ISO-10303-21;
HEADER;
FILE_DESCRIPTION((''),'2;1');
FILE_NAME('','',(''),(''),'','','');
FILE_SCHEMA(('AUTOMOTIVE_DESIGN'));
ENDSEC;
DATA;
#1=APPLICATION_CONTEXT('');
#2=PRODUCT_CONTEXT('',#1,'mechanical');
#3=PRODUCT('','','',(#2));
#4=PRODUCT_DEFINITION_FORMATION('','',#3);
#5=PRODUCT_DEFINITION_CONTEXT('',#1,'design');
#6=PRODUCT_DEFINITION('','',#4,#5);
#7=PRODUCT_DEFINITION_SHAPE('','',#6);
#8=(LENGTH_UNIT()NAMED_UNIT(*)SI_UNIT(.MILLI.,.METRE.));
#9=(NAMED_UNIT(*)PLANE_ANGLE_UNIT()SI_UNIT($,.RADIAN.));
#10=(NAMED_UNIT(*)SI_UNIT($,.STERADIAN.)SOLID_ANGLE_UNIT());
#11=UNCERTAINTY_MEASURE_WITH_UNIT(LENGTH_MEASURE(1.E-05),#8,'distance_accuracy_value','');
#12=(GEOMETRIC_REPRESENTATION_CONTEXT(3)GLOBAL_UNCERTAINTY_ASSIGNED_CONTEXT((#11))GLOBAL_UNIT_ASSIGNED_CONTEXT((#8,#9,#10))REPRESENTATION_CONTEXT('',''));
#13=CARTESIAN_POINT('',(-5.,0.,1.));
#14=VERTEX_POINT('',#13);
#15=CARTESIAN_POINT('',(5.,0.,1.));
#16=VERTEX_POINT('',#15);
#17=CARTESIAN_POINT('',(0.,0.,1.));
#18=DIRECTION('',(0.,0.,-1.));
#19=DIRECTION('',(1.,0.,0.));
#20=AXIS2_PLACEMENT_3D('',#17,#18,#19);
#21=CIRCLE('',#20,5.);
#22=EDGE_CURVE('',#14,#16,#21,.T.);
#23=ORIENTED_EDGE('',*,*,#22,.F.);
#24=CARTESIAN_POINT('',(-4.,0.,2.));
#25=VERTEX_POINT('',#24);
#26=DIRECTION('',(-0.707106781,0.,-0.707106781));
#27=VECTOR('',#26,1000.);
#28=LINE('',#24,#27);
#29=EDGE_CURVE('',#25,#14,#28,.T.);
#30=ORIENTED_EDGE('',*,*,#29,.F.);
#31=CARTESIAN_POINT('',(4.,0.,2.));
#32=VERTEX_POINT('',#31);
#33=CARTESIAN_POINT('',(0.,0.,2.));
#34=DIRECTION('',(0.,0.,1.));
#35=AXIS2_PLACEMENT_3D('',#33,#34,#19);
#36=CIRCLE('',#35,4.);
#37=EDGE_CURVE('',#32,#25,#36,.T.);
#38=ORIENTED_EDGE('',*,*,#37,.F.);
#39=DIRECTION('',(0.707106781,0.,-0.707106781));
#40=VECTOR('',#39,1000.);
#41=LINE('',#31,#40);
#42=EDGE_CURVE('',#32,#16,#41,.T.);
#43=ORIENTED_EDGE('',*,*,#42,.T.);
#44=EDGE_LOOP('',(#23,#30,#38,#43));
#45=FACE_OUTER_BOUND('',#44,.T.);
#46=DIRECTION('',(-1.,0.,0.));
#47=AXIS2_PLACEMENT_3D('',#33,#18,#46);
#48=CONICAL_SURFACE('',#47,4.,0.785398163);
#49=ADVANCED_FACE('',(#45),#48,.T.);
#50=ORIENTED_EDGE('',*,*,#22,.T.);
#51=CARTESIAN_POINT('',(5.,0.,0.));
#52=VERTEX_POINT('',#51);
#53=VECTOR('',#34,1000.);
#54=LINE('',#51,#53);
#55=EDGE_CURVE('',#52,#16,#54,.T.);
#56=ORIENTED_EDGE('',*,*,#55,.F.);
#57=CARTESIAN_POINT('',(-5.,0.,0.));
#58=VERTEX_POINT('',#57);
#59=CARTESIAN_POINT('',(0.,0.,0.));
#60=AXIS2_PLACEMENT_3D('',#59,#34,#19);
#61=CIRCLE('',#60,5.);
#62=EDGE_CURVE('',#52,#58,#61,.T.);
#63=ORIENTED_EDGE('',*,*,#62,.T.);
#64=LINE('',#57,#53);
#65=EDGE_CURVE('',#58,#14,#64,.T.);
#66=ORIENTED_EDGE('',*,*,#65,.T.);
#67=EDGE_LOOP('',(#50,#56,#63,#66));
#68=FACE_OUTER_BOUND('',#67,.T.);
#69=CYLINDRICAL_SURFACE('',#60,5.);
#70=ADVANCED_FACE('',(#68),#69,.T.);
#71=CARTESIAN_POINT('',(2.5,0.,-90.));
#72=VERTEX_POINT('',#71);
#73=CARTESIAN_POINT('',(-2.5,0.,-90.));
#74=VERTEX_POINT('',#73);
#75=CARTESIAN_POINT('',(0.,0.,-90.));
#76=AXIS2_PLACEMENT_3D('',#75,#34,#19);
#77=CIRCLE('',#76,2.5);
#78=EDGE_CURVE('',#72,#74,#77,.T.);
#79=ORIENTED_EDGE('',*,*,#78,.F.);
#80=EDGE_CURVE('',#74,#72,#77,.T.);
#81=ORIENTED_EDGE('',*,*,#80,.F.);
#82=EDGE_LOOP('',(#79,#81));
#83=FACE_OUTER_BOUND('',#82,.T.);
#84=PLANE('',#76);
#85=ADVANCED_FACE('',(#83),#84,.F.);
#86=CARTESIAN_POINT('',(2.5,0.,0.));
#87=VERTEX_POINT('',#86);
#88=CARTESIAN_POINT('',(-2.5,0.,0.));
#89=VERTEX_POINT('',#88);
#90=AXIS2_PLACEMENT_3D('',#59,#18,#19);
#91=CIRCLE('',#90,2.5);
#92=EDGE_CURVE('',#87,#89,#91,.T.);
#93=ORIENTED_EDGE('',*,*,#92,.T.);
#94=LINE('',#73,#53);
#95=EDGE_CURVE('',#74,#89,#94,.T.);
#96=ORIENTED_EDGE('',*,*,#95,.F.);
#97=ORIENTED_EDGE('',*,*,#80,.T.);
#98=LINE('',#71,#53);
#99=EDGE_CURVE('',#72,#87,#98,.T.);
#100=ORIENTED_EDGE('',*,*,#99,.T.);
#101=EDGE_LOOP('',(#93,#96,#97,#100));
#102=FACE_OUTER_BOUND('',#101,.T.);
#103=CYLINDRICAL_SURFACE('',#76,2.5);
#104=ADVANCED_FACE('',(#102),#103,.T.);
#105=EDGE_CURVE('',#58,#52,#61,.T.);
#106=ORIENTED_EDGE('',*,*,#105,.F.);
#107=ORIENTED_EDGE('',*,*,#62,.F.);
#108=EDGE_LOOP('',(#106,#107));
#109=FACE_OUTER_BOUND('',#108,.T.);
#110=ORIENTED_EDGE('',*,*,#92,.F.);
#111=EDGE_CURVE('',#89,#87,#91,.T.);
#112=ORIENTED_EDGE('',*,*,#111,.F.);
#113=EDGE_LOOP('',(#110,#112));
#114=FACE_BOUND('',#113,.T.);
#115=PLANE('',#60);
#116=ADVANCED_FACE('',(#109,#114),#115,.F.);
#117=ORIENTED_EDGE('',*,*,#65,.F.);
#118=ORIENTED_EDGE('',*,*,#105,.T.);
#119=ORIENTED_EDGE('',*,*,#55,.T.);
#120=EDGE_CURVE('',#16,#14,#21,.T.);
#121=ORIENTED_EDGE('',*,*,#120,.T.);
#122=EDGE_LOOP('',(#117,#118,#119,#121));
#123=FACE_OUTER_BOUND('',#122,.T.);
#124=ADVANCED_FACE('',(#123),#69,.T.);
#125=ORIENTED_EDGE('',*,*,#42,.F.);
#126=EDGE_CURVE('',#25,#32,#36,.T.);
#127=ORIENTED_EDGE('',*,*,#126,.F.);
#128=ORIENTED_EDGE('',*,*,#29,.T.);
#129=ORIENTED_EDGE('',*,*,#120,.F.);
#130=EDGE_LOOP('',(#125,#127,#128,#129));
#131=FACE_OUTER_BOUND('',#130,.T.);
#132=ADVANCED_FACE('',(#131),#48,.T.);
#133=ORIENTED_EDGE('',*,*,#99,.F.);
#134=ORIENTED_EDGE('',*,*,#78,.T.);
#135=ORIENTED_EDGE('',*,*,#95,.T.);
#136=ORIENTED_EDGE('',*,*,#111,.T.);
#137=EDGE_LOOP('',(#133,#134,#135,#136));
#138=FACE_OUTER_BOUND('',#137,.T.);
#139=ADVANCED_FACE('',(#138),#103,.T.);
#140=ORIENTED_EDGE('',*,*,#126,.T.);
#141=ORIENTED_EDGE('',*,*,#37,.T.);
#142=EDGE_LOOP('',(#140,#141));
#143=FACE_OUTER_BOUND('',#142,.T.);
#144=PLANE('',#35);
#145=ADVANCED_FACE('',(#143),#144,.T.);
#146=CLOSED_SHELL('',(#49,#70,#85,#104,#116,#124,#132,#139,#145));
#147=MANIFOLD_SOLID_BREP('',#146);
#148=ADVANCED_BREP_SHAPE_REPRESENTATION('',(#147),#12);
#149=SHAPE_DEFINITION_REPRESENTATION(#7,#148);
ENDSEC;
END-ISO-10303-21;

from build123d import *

# Parameters (mm, degrees)
BOSS_EXTRUDE1_DEPTH      = 2
BOSS_EXTRUDE1_DEPTH_BACK = 90
SKETCH1_R                = 2.5
SKETCH2_R                = 5
BOSS_EXTRUDE2_DEPTH      = 2
CHAMFER1_SIZE            = 1


with BuildPart() as part:
    # Sketch1 → Boss-Extrude1 (new, two sides: drawn at the far end of the back side and taken through both)
    with BuildSketch(Plane.XY.offset(-BOSS_EXTRUDE1_DEPTH_BACK)):
        Circle(SKETCH1_R)
    extrude(amount=BOSS_EXTRUDE1_DEPTH + BOSS_EXTRUDE1_DEPTH_BACK)

    # Sketch2 → Boss-Extrude2 (add)
    with BuildSketch(Plane.XY.offset(2)):
        Circle(SKETCH2_R)
    extrude(amount=-BOSS_EXTRUDE2_DEPTH)

    # Chamfer1
    chamfer1_edges = [part.edges().sort_by_distance(p)[0] for p in [
        (-5, 0, 2),
    ]]
    chamfer(chamfer1_edges, length=CHAMFER1_SIZE)


solid = part.part
